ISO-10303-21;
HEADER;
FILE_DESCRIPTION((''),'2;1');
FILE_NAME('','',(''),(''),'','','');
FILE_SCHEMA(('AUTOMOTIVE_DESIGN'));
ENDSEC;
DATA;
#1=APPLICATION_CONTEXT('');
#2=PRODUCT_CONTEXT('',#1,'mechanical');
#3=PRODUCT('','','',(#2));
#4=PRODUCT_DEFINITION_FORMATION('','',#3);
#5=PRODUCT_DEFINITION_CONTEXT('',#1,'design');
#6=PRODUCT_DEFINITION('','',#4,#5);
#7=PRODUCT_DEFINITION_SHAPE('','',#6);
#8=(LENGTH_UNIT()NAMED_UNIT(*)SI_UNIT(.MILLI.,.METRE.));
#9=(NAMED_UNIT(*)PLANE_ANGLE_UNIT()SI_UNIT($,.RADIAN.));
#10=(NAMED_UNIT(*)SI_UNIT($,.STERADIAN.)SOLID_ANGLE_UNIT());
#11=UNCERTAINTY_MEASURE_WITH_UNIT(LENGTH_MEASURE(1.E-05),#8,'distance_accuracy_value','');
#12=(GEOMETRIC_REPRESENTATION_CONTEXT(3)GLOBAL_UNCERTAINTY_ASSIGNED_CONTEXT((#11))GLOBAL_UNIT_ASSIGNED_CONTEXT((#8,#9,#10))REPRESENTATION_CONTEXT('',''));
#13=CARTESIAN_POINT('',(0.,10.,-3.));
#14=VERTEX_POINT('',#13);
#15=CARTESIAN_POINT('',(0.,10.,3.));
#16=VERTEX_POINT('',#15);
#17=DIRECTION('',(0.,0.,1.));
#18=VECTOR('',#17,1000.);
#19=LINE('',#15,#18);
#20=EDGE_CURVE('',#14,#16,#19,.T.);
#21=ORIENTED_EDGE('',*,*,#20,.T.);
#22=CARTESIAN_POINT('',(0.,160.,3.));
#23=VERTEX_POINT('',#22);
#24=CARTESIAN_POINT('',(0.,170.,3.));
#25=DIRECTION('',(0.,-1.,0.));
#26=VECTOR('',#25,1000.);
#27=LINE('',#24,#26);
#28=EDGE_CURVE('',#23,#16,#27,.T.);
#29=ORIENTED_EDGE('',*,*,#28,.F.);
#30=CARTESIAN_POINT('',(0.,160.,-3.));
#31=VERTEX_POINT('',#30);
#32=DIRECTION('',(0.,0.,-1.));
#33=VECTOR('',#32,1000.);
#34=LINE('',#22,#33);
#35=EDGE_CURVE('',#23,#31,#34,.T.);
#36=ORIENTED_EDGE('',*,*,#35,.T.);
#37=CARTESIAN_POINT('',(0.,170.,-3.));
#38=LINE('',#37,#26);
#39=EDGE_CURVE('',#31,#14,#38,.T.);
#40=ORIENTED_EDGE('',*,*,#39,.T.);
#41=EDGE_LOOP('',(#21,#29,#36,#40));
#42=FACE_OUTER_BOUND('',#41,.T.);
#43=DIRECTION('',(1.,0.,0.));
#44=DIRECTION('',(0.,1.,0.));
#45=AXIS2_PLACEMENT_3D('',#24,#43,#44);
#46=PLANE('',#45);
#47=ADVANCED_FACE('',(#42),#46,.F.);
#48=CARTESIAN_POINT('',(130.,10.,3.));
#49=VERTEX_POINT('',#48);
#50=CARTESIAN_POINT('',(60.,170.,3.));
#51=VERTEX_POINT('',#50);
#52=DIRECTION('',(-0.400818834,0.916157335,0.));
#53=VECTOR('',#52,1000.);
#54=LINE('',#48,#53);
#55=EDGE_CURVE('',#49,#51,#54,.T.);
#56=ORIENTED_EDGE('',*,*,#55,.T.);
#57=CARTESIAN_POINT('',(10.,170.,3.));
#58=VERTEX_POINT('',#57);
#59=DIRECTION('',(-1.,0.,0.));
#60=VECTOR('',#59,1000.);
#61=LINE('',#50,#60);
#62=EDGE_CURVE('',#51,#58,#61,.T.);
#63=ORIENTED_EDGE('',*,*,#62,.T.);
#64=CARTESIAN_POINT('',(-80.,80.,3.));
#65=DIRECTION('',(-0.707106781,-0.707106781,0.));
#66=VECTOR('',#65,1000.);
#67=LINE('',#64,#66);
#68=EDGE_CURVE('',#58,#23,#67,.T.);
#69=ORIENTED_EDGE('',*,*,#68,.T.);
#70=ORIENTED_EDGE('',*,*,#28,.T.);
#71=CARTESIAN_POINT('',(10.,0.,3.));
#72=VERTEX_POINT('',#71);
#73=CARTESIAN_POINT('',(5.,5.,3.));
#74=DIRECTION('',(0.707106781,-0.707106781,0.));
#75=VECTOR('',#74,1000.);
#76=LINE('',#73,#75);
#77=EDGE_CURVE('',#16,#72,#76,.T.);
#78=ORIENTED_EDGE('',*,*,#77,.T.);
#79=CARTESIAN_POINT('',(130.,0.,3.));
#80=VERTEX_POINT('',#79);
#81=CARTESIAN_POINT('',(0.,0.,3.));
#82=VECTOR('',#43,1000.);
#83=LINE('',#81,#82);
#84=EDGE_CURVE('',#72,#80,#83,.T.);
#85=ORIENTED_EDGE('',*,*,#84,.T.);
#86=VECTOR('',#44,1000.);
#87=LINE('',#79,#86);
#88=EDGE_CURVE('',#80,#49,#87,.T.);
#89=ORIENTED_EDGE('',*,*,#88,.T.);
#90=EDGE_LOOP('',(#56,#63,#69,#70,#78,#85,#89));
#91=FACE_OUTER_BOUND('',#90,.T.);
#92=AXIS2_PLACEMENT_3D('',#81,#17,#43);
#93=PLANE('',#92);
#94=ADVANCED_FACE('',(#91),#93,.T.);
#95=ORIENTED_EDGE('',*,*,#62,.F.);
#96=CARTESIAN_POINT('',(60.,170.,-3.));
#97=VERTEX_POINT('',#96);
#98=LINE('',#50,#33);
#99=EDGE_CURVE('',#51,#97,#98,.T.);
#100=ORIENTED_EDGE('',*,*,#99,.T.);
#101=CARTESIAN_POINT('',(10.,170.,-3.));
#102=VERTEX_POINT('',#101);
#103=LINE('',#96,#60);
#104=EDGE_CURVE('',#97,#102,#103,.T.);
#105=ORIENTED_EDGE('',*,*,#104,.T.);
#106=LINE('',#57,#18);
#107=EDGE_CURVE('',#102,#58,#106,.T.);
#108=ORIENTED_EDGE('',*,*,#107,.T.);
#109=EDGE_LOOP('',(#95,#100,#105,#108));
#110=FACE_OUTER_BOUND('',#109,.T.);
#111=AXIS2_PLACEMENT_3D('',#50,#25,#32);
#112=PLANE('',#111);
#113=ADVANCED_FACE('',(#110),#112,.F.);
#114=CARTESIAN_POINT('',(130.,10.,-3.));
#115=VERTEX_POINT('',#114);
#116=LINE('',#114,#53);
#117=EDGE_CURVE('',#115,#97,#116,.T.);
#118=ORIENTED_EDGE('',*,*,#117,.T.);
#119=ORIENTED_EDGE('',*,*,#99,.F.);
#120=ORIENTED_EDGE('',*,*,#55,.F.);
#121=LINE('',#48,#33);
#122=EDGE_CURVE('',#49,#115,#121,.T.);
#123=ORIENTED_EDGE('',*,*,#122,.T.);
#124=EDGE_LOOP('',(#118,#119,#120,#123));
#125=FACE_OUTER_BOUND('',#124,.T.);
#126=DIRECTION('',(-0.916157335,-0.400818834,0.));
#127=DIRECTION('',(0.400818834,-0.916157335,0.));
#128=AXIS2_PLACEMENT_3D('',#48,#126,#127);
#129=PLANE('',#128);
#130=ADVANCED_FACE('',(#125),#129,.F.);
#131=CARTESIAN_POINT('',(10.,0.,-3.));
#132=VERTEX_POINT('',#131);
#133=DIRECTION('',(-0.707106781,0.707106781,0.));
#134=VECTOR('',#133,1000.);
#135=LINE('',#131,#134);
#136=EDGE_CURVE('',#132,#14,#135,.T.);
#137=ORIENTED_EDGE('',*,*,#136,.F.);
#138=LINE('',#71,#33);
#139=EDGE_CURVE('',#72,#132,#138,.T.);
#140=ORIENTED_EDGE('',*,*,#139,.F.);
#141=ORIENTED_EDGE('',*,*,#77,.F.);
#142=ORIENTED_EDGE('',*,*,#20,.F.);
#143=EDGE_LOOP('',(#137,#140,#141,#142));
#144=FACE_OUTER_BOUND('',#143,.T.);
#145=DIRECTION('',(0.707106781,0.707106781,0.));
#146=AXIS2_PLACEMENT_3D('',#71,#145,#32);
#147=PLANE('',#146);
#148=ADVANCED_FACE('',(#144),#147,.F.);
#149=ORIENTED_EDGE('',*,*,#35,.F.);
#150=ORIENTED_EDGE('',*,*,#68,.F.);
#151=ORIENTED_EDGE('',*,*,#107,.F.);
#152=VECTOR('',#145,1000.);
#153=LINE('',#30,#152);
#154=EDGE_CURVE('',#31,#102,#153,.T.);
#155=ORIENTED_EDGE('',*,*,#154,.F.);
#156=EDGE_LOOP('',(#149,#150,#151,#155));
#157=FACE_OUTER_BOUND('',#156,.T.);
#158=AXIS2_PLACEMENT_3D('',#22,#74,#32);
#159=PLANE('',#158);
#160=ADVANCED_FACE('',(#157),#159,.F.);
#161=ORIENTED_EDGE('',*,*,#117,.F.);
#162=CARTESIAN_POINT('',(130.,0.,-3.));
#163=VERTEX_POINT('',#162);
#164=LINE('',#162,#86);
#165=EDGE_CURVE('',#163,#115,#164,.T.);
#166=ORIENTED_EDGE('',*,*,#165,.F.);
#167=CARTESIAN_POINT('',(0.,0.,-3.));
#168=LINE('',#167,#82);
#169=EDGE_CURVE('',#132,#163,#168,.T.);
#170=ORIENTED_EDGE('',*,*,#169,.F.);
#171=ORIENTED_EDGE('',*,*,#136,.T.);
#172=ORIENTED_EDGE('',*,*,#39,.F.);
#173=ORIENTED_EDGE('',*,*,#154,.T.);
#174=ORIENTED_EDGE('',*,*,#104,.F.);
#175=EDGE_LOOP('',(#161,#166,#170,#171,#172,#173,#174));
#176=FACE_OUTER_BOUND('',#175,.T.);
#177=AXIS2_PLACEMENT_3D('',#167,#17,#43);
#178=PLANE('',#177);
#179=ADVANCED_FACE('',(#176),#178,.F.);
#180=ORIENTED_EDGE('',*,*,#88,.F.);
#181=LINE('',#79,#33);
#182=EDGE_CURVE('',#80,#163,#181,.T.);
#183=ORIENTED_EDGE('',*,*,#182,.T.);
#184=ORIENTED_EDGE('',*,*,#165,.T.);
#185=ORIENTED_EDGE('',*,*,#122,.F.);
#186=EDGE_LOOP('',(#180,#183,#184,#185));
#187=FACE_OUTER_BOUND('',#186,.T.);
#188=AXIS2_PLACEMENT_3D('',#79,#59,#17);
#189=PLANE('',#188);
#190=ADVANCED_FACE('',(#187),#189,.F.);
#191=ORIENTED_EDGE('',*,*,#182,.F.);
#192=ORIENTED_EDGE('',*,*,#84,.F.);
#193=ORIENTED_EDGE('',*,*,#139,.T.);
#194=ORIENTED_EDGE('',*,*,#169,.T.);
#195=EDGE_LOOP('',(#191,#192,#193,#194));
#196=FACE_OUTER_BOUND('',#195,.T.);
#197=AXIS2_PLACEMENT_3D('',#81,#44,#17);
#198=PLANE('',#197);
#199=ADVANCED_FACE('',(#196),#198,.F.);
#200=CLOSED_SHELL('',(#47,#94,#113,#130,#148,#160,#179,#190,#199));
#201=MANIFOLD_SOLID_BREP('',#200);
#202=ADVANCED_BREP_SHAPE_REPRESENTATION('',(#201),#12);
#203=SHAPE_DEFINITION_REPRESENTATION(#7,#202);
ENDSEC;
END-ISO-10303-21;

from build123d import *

# Parameters (mm, degrees)
BOSS_EXTRUDE1_DEPTH = 3
CHAMFER1_SIZE       = 10


with BuildPart() as part:
    # Sketch1 → Boss-Extrude1 (new, symmetric)
    with BuildSketch(Plane.XY):
        Polygon((0, 170), (0, 0), (130, 0), (130, 10), (60, 170), align=None)
    extrude(amount=BOSS_EXTRUDE1_DEPTH, both=True)

    # Chamfer1
    chamfer1_edges = [part.edges().sort_by_distance(p)[0] for p in [
        (0, 0, 0),
        (0, 170, 0),
    ]]
    chamfer(chamfer1_edges, length=CHAMFER1_SIZE)


solid = part.part
